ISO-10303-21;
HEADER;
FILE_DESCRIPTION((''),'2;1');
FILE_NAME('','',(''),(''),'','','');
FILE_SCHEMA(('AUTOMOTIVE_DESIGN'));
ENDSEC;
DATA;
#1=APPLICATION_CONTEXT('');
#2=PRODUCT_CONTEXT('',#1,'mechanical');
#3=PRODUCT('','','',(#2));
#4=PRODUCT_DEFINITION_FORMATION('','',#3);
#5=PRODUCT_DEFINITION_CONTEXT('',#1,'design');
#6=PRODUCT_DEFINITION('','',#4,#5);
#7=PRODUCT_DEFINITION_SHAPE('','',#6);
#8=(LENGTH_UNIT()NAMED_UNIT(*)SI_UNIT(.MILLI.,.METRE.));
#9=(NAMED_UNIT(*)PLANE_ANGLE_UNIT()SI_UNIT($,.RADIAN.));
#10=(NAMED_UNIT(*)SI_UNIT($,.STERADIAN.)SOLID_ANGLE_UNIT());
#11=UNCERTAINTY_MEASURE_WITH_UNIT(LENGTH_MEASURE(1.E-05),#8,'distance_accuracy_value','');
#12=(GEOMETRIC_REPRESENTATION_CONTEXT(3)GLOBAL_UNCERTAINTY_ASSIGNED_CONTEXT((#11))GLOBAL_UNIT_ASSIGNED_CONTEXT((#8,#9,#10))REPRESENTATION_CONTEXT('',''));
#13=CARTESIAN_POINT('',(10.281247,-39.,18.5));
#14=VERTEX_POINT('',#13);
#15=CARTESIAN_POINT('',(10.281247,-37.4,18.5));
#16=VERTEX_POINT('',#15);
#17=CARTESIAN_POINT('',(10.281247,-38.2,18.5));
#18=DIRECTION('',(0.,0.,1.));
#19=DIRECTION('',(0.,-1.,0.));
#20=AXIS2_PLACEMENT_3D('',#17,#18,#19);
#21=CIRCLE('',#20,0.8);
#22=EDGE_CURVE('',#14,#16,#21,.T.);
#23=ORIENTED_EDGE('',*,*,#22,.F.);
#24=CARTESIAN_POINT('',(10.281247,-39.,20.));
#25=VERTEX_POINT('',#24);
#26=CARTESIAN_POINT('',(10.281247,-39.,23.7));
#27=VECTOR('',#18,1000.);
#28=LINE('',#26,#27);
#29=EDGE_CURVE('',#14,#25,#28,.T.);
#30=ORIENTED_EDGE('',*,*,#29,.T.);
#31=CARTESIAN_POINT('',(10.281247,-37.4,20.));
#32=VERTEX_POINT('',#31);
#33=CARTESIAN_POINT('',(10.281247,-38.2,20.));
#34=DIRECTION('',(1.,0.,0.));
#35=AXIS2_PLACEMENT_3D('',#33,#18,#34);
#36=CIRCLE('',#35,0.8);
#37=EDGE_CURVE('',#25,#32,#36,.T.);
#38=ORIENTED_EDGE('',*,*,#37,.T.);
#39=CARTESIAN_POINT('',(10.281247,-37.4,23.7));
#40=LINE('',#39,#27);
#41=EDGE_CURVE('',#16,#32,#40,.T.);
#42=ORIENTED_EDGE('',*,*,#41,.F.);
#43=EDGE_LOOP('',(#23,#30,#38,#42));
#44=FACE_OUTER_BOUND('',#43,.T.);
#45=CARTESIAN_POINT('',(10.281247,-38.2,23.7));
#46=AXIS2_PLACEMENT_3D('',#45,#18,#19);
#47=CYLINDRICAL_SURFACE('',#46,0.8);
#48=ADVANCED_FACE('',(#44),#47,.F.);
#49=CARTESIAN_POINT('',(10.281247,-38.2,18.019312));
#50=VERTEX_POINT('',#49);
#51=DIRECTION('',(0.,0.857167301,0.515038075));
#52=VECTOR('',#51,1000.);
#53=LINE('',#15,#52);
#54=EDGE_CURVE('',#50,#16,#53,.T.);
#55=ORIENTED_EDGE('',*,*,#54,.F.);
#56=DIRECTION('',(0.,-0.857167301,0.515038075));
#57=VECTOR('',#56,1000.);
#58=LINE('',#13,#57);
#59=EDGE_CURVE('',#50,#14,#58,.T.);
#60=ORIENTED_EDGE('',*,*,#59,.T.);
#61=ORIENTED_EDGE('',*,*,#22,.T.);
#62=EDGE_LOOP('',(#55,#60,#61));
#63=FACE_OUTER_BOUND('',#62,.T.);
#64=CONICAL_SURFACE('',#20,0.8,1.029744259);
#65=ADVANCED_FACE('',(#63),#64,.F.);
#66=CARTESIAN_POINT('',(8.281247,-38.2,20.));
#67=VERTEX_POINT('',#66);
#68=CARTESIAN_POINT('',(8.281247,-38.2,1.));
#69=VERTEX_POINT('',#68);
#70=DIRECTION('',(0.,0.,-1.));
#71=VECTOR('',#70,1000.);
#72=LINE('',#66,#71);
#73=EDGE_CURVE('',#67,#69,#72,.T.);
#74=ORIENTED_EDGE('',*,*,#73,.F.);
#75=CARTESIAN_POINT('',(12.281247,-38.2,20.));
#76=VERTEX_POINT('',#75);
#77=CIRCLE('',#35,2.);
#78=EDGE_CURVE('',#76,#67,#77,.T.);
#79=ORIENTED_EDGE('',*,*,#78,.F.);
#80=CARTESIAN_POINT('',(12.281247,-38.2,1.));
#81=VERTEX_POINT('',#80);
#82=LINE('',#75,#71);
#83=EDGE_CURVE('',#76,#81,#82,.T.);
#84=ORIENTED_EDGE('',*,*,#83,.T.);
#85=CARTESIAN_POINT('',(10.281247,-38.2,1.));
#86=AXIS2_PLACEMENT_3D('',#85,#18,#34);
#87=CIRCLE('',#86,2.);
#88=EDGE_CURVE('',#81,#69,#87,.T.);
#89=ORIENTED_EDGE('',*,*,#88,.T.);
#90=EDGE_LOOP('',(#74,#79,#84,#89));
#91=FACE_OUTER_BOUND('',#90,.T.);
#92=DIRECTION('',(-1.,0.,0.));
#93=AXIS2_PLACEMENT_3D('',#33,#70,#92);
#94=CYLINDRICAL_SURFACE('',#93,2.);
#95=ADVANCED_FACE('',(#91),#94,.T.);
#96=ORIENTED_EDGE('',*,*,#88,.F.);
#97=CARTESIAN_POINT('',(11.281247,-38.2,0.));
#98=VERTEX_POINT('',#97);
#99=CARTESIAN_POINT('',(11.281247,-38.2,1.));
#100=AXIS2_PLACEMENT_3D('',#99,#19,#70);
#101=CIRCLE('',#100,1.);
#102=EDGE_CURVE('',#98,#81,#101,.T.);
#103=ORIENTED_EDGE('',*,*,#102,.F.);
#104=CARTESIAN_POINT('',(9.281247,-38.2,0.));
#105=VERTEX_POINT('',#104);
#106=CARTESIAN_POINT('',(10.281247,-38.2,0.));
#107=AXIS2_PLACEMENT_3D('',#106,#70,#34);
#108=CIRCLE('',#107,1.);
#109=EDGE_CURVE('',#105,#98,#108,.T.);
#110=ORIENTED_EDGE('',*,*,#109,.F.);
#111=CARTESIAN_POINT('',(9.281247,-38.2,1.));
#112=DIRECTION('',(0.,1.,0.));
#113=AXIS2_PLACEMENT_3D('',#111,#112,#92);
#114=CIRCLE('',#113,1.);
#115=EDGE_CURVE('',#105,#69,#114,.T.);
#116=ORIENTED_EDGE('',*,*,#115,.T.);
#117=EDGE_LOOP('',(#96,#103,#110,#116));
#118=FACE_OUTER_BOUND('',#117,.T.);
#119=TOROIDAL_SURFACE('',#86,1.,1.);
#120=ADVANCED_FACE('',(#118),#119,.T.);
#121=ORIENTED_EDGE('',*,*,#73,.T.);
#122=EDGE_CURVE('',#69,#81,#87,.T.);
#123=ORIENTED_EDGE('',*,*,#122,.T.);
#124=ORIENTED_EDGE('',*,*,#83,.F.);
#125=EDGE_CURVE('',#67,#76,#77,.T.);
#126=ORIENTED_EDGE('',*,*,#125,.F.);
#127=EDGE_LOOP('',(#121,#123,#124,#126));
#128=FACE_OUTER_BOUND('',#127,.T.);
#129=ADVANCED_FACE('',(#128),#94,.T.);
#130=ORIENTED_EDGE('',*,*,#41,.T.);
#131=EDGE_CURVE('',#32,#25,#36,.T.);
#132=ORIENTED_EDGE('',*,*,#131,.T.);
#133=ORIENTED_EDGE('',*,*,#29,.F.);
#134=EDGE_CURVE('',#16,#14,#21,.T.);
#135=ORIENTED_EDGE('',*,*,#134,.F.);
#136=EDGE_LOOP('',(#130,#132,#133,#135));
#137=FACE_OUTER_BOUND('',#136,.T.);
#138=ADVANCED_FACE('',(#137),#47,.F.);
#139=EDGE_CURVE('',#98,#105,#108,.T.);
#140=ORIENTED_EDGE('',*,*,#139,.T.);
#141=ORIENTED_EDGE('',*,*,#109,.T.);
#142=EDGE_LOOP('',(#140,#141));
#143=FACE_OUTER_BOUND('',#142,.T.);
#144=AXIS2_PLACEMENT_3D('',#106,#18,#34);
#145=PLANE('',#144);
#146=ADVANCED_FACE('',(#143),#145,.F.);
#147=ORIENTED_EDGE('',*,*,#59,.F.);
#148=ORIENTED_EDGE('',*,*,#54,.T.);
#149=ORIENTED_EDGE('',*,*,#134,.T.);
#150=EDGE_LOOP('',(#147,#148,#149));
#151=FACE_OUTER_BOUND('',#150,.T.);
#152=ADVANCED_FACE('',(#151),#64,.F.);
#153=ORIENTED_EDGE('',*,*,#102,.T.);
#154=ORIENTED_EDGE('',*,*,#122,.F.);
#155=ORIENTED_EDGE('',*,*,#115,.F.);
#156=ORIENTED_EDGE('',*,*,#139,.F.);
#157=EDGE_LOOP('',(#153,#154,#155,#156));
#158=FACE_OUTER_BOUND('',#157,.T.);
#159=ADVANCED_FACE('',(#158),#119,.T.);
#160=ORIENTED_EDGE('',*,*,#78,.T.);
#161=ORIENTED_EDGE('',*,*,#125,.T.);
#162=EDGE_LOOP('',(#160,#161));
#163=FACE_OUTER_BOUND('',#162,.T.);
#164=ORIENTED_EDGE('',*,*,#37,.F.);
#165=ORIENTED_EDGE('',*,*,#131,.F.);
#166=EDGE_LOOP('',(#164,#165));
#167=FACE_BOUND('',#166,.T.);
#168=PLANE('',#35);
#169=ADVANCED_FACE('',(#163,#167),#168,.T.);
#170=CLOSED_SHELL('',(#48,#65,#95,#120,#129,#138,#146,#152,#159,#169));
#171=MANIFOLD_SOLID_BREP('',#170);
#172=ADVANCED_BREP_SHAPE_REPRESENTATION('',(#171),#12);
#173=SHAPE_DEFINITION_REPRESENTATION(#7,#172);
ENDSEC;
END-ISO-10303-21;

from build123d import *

# Parameters (mm, degrees)
SKETCH1_R             = 2
BOSS_EXTRUDE1_DEPTH   = 20
M2_TAPPED_HOLE1_D     = 1.6
M2_TAPPED_HOLE1_DEPTH = 5.2
M2_TAPPED_HOLE1_TIP   = 0.480688495
FILLET1_R             = 1


with BuildPart() as part:
    # Sketch1 → Boss-Extrude1 (new body)
    with BuildSketch(Plane.XY):
        with Locations((10.281246694, -38.2)):
            Circle(SKETCH1_R)
    extrude(amount=BOSS_EXTRUDE1_DEPTH)

    # M2 Tapped Hole1
    with Locations(Plane(origin=(10.281246694, -38.2, 23.7), x_dir=(0, 1, 0), z_dir=(0, 0, 1))):
        with Locations((0, 0)):
            Hole(M2_TAPPED_HOLE1_D / 2, depth=M2_TAPPED_HOLE1_DEPTH)
            with Locations((0, 0, -(M2_TAPPED_HOLE1_DEPTH + M2_TAPPED_HOLE1_TIP / 2))):  # 118° drill point
                Cone(0, M2_TAPPED_HOLE1_D / 2, M2_TAPPED_HOLE1_TIP, mode=Mode.SUBTRACT)

    # Fillet1
    fillet1_edges = [part.edges().sort_by_distance(p)[0] for p in [
        (8.281246694, -38.2, 0),
    ]]
    fillet(fillet1_edges, radius=FILLET1_R)


solid = part.part
